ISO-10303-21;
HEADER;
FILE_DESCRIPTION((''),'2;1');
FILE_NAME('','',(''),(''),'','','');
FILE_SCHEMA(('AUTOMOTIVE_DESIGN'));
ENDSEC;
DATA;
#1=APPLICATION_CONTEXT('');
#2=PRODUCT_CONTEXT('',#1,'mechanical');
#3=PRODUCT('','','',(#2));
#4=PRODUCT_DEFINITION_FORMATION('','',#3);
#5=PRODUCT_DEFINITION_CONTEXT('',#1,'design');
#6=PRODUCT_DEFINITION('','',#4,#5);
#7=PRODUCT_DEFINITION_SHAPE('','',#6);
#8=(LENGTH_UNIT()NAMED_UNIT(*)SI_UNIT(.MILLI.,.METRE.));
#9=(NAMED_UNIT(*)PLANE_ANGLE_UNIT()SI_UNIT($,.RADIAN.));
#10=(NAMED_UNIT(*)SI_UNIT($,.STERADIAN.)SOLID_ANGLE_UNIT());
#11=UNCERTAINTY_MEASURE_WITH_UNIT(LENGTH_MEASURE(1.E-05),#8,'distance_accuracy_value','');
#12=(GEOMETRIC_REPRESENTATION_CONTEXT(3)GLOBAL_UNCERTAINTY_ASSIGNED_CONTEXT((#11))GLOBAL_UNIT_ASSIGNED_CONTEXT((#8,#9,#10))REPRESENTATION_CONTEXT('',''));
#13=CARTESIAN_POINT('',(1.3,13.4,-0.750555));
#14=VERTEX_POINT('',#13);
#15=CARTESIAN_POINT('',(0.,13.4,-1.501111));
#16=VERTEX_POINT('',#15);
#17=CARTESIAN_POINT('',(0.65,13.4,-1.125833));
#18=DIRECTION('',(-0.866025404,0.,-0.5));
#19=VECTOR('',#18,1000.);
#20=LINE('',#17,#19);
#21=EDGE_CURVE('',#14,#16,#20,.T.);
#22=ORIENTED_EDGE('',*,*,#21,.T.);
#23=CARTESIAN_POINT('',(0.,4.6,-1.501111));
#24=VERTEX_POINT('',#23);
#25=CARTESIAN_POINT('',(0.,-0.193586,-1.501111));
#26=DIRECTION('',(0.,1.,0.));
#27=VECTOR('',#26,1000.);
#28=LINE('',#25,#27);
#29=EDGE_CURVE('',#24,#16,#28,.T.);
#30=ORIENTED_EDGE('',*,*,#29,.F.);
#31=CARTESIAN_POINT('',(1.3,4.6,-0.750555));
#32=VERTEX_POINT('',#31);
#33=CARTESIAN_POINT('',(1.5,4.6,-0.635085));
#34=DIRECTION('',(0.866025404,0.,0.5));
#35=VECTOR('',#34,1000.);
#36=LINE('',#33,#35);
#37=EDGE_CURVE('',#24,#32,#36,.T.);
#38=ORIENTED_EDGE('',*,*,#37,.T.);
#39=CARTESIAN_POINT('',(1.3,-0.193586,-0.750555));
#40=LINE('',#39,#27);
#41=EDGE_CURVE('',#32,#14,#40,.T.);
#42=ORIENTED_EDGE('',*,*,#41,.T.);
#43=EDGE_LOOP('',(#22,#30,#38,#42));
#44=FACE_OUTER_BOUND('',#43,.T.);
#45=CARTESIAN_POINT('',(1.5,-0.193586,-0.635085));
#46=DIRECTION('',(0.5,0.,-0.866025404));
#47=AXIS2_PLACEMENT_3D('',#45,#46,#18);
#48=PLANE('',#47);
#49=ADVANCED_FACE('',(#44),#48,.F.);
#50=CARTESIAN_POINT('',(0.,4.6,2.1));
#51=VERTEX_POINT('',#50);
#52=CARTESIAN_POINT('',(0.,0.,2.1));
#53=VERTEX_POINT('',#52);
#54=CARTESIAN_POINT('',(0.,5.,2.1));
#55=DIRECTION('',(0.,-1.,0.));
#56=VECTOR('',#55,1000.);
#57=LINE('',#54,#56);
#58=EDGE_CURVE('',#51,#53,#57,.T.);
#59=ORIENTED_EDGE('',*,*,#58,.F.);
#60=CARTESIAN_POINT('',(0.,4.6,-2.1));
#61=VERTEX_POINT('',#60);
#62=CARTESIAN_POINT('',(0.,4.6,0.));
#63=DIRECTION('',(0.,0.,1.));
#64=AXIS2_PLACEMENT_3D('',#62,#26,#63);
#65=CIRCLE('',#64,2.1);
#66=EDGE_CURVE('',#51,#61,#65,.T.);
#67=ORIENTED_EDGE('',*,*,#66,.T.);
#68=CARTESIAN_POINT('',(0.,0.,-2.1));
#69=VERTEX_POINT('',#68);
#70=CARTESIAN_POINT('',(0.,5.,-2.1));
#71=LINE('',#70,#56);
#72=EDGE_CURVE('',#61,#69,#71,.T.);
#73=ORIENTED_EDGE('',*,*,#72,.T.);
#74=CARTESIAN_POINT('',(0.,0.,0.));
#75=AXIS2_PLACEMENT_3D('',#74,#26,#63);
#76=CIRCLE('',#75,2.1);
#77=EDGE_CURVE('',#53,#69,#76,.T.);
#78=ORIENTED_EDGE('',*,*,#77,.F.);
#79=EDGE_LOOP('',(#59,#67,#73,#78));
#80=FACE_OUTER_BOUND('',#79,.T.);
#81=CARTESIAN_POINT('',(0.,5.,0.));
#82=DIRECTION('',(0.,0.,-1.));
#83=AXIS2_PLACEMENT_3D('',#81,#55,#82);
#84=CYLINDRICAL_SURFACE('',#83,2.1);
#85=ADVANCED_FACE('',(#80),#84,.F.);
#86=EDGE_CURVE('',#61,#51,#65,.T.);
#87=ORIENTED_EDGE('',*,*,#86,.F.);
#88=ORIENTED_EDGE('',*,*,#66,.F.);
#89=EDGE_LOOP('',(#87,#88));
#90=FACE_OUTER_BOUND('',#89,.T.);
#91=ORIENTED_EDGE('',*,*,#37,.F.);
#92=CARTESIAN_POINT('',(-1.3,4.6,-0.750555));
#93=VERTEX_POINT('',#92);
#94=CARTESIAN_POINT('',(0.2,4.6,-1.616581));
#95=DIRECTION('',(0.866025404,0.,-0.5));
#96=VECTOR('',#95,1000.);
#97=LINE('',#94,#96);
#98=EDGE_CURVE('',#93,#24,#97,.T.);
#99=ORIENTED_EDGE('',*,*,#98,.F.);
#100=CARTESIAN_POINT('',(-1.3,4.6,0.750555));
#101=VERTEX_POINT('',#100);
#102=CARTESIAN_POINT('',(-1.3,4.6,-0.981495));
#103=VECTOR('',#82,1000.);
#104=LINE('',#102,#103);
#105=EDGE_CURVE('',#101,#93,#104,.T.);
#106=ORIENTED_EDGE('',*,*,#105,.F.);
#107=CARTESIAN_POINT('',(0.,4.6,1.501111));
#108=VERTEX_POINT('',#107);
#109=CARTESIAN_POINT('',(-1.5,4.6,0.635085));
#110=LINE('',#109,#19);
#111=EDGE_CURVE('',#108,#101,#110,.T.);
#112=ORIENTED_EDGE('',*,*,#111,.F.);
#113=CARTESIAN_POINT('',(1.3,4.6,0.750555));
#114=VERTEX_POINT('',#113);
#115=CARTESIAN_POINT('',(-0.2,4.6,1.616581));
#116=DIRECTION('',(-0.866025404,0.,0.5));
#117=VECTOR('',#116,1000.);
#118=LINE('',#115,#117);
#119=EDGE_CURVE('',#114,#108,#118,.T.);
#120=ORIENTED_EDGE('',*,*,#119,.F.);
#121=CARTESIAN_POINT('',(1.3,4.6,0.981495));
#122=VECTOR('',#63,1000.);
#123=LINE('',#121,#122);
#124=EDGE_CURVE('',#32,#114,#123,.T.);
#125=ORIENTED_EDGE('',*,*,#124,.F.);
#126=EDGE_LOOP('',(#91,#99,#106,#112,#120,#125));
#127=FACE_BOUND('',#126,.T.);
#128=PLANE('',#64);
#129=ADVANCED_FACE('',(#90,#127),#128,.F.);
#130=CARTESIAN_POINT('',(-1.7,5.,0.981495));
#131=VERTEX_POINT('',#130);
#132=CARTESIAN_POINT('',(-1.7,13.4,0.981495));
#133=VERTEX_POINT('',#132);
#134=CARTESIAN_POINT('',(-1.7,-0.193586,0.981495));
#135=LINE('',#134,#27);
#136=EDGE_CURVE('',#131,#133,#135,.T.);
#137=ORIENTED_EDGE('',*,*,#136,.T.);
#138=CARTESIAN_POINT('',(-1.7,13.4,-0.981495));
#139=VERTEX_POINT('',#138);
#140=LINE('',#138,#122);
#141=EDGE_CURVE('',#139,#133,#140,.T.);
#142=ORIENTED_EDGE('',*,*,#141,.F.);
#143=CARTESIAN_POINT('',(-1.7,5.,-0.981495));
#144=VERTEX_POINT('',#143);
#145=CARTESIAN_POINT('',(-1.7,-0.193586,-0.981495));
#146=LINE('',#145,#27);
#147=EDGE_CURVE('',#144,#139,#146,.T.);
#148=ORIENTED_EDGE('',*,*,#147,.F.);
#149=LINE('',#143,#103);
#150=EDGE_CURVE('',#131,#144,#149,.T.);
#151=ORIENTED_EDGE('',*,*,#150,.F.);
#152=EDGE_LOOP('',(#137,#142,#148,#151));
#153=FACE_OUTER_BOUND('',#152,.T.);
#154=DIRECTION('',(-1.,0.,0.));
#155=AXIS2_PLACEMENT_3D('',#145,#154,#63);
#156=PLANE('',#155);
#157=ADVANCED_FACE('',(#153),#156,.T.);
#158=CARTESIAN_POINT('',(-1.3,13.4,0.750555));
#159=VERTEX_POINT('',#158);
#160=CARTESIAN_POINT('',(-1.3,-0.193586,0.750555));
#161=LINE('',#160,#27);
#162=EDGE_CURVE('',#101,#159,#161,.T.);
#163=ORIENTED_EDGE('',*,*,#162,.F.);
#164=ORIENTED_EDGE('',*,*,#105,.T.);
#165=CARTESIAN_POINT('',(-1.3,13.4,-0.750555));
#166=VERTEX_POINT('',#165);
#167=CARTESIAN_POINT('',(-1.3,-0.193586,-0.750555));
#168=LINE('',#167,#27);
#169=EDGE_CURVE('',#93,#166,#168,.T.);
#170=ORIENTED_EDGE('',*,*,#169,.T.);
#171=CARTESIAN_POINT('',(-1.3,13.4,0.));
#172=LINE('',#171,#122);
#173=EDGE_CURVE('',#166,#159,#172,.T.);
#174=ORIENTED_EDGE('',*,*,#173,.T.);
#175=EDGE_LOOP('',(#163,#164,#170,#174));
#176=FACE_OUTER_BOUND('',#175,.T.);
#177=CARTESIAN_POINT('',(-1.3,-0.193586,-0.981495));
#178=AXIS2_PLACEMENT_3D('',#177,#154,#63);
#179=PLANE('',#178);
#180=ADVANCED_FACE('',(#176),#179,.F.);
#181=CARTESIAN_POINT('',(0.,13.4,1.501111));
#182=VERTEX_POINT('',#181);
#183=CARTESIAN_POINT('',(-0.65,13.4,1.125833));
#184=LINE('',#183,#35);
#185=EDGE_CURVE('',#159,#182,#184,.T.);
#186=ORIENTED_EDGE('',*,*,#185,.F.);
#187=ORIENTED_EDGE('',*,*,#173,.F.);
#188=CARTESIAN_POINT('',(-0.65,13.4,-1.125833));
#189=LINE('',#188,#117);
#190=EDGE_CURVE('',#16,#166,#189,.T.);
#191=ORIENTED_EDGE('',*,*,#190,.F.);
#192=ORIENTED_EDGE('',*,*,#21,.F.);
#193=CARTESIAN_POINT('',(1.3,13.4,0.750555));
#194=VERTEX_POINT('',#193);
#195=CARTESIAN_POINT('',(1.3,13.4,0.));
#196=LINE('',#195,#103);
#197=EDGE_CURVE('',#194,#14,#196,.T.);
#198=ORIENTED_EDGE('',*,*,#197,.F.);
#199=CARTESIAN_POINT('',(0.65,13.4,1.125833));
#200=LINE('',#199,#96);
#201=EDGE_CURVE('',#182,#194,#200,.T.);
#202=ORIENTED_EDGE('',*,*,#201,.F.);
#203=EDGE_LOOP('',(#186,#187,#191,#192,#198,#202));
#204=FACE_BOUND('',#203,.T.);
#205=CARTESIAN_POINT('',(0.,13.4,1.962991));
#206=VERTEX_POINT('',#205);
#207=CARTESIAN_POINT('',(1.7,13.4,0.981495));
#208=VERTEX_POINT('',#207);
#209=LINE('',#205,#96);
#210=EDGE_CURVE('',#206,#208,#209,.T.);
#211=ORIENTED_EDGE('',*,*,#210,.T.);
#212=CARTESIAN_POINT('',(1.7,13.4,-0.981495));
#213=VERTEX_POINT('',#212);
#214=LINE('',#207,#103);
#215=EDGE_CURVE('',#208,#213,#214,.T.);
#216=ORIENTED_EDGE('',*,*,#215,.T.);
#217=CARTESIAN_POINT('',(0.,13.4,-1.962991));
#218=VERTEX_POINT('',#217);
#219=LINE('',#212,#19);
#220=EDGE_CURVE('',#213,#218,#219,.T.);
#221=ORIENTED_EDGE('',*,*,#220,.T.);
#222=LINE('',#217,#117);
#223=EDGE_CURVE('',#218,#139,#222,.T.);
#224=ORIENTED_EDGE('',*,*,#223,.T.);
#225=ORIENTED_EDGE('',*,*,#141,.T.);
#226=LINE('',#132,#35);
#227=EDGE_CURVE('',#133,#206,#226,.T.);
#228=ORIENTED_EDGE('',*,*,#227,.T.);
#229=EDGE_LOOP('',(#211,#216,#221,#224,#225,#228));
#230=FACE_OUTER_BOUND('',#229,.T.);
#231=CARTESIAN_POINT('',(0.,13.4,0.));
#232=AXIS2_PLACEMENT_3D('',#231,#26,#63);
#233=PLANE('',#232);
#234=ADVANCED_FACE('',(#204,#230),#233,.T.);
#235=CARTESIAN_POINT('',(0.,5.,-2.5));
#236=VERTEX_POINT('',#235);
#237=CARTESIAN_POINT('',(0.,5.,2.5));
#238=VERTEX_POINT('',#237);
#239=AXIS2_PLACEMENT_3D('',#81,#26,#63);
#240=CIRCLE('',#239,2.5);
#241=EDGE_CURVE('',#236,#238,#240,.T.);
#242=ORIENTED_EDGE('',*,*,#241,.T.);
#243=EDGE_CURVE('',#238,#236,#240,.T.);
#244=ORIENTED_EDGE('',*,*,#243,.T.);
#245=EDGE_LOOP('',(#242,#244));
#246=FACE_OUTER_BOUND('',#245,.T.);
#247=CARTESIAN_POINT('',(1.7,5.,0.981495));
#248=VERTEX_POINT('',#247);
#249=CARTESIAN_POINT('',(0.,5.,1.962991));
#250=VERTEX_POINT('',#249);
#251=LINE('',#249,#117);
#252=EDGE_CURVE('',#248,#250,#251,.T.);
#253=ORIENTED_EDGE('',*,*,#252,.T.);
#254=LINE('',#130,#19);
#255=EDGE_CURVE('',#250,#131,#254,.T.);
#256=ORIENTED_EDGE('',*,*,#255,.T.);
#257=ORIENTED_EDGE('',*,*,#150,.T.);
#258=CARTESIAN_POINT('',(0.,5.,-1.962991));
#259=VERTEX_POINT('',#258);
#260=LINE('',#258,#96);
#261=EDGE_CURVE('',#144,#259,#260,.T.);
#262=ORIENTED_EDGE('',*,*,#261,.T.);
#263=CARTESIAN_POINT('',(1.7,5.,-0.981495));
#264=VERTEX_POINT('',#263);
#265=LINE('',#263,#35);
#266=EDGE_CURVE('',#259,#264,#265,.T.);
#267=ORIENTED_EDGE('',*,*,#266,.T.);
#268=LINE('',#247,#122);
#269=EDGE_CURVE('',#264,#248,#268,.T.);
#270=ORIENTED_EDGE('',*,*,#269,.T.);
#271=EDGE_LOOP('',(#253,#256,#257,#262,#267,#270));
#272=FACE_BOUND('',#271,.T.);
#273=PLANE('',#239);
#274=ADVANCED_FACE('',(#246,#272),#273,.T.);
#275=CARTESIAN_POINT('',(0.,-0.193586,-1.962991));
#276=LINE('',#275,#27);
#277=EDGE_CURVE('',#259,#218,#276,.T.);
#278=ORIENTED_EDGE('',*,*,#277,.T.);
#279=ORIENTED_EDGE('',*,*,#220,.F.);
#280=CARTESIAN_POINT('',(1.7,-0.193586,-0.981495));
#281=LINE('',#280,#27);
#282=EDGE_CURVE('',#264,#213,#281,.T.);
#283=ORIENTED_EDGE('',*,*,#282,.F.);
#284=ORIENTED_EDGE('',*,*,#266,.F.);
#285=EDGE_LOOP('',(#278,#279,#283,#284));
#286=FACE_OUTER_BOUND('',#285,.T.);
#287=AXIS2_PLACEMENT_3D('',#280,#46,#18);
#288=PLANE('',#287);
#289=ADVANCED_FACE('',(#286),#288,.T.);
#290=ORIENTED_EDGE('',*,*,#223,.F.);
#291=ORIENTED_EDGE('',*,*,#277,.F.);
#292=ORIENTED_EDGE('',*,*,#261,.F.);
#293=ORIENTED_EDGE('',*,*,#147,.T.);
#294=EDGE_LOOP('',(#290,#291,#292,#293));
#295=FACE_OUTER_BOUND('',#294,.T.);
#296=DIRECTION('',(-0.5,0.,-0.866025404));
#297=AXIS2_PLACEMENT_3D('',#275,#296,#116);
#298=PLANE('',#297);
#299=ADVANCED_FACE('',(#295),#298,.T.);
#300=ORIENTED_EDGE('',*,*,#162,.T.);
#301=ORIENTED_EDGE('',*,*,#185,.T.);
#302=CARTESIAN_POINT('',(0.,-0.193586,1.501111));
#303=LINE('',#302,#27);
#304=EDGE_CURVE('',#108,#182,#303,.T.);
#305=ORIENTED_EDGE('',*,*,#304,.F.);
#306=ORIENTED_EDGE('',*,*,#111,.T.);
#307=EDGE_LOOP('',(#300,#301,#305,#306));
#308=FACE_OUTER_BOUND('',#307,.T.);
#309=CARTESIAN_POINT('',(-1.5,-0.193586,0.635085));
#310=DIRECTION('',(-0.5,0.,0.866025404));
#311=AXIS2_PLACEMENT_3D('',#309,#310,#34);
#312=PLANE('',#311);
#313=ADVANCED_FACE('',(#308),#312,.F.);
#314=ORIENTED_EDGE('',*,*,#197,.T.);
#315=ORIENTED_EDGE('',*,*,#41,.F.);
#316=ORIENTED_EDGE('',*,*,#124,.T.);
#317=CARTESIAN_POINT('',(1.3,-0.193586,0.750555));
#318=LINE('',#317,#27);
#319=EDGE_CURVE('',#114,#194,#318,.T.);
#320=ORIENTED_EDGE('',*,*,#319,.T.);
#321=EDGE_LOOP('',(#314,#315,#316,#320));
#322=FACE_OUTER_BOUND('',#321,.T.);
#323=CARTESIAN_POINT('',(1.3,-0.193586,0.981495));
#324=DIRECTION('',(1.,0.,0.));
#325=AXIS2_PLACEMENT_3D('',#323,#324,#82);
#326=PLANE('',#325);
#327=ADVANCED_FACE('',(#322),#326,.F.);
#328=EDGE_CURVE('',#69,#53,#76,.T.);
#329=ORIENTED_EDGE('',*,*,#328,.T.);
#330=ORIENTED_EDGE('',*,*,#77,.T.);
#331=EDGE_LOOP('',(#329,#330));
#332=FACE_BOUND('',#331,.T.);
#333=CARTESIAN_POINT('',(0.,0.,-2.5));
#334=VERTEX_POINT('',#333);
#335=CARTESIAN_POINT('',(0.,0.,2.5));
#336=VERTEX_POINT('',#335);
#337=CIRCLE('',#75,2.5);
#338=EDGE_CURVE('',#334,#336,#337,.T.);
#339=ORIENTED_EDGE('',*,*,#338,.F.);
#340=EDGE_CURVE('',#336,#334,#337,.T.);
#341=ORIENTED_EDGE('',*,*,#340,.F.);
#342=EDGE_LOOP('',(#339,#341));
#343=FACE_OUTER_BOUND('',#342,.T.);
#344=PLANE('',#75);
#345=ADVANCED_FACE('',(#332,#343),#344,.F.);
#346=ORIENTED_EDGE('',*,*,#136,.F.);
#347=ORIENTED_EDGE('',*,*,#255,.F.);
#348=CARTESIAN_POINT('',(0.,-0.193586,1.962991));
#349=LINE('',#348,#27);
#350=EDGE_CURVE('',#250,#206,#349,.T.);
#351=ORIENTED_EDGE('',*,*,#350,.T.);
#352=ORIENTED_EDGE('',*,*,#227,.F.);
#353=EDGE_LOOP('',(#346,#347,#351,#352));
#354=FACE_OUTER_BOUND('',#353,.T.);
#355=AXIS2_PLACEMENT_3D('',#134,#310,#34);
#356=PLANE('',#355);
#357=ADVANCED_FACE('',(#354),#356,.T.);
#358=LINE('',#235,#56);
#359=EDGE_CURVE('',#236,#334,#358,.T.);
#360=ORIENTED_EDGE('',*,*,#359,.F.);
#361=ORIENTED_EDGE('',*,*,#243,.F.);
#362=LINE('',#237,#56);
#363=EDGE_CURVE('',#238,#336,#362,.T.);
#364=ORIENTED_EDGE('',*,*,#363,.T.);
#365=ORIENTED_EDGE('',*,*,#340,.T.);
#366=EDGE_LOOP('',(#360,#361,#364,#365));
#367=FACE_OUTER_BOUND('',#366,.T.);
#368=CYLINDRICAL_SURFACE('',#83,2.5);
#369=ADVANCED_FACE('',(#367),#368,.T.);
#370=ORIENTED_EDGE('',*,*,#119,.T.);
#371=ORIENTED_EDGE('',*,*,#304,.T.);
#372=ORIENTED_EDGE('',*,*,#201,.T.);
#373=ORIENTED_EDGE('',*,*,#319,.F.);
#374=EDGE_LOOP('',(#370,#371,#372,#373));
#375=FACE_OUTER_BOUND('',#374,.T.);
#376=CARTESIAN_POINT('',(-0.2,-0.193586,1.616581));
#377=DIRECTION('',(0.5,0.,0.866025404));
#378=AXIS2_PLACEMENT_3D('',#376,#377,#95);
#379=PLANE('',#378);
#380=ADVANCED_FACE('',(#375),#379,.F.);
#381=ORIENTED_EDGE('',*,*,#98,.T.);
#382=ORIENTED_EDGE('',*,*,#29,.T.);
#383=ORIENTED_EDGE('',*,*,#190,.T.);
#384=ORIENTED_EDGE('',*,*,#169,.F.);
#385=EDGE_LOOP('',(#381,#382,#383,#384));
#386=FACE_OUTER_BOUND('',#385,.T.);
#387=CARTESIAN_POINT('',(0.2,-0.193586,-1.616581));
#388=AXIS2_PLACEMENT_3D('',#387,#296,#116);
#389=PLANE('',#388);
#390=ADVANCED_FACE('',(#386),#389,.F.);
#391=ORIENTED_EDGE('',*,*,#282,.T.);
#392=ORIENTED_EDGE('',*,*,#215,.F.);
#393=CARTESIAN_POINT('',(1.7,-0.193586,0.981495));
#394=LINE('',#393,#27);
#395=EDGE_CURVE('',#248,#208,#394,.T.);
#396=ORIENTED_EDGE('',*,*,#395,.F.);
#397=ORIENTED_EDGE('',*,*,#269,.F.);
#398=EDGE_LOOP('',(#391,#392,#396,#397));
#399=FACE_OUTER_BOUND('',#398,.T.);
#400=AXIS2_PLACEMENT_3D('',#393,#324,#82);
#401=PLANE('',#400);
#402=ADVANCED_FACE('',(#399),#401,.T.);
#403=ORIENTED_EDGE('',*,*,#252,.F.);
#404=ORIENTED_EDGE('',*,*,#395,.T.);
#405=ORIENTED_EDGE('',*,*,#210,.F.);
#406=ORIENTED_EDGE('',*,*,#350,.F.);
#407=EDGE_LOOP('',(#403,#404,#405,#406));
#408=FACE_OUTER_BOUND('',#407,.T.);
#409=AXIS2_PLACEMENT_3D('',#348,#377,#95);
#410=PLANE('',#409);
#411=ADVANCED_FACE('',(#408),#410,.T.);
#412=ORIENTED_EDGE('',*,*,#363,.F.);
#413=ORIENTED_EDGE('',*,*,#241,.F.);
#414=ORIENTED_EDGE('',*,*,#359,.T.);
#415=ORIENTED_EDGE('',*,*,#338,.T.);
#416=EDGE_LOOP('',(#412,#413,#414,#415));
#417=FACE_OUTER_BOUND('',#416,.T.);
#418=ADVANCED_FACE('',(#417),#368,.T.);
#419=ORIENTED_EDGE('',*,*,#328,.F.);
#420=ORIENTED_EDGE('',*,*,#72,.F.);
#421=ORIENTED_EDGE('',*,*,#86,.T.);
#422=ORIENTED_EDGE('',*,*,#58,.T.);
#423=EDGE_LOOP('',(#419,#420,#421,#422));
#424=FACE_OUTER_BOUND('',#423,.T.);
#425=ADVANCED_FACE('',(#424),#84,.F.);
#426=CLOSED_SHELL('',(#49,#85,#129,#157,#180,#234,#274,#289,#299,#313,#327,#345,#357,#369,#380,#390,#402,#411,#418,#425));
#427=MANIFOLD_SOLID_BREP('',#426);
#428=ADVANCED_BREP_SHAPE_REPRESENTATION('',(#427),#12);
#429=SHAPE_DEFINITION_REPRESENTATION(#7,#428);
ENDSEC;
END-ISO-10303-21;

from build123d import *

# Parameters (mm, degrees)
BOSS_EXTRUDE3_DEPTH = 5
BOSS_EXTRUDE4_DEPTH = 8.4
SHELL1_T            = -0.4


with BuildPart() as part:
    # Sketch1 → Boss-Extrude3 (new body)
    with BuildSketch(Plane(origin=(0, 0, 0), x_dir=(1, 0, 0), z_dir=(0, 1, 0))):
        with BuildLine():
            ThreePointArc((0, 2.5), (-1.25, 2.165063509), (-2.165063509, 1.25))
            ThreePointArc((-2.165063509, 1.25), (-2.5, 0), (-2.165063509, -1.25))
            ThreePointArc((-2.165063509, -1.25), (-1.25, -2.165063509), (0, -2.5))
            ThreePointArc((0, -2.5), (1.25, -2.165063509), (2.165063509, -1.25))
            ThreePointArc((2.165063509, -1.25), (2.5, 0), (2.165063509, 1.25))
            ThreePointArc((2.165063509, 1.25), (1.25, 2.165063509), (0, 2.5))
        make_face()
    extrude(amount=BOSS_EXTRUDE3_DEPTH)

    # Sketch2 → Boss-Extrude4 (add)
    with BuildSketch(Plane(origin=(0, 13.4, 0), x_dir=(1, 0, 0), z_dir=(0, 1, 0))):
        Polygon((0, 1.962990915), (-1.7, 0.981495458), (-1.7, -0.981495458), (0, -1.962990915), (1.7, -0.981495458), (1.7, 0.981495458), align=None)
    extrude(amount=-BOSS_EXTRUDE4_DEPTH)

    # Shell1
    shell1_openings = [part.faces().sort_by_distance(p)[0] for p in [
        (0, 13.4, 0),
        (0, 0, 0),
    ]]
    offset(amount=SHELL1_T, openings=shell1_openings, kind=Kind.INTERSECTION)


solid = part.part
